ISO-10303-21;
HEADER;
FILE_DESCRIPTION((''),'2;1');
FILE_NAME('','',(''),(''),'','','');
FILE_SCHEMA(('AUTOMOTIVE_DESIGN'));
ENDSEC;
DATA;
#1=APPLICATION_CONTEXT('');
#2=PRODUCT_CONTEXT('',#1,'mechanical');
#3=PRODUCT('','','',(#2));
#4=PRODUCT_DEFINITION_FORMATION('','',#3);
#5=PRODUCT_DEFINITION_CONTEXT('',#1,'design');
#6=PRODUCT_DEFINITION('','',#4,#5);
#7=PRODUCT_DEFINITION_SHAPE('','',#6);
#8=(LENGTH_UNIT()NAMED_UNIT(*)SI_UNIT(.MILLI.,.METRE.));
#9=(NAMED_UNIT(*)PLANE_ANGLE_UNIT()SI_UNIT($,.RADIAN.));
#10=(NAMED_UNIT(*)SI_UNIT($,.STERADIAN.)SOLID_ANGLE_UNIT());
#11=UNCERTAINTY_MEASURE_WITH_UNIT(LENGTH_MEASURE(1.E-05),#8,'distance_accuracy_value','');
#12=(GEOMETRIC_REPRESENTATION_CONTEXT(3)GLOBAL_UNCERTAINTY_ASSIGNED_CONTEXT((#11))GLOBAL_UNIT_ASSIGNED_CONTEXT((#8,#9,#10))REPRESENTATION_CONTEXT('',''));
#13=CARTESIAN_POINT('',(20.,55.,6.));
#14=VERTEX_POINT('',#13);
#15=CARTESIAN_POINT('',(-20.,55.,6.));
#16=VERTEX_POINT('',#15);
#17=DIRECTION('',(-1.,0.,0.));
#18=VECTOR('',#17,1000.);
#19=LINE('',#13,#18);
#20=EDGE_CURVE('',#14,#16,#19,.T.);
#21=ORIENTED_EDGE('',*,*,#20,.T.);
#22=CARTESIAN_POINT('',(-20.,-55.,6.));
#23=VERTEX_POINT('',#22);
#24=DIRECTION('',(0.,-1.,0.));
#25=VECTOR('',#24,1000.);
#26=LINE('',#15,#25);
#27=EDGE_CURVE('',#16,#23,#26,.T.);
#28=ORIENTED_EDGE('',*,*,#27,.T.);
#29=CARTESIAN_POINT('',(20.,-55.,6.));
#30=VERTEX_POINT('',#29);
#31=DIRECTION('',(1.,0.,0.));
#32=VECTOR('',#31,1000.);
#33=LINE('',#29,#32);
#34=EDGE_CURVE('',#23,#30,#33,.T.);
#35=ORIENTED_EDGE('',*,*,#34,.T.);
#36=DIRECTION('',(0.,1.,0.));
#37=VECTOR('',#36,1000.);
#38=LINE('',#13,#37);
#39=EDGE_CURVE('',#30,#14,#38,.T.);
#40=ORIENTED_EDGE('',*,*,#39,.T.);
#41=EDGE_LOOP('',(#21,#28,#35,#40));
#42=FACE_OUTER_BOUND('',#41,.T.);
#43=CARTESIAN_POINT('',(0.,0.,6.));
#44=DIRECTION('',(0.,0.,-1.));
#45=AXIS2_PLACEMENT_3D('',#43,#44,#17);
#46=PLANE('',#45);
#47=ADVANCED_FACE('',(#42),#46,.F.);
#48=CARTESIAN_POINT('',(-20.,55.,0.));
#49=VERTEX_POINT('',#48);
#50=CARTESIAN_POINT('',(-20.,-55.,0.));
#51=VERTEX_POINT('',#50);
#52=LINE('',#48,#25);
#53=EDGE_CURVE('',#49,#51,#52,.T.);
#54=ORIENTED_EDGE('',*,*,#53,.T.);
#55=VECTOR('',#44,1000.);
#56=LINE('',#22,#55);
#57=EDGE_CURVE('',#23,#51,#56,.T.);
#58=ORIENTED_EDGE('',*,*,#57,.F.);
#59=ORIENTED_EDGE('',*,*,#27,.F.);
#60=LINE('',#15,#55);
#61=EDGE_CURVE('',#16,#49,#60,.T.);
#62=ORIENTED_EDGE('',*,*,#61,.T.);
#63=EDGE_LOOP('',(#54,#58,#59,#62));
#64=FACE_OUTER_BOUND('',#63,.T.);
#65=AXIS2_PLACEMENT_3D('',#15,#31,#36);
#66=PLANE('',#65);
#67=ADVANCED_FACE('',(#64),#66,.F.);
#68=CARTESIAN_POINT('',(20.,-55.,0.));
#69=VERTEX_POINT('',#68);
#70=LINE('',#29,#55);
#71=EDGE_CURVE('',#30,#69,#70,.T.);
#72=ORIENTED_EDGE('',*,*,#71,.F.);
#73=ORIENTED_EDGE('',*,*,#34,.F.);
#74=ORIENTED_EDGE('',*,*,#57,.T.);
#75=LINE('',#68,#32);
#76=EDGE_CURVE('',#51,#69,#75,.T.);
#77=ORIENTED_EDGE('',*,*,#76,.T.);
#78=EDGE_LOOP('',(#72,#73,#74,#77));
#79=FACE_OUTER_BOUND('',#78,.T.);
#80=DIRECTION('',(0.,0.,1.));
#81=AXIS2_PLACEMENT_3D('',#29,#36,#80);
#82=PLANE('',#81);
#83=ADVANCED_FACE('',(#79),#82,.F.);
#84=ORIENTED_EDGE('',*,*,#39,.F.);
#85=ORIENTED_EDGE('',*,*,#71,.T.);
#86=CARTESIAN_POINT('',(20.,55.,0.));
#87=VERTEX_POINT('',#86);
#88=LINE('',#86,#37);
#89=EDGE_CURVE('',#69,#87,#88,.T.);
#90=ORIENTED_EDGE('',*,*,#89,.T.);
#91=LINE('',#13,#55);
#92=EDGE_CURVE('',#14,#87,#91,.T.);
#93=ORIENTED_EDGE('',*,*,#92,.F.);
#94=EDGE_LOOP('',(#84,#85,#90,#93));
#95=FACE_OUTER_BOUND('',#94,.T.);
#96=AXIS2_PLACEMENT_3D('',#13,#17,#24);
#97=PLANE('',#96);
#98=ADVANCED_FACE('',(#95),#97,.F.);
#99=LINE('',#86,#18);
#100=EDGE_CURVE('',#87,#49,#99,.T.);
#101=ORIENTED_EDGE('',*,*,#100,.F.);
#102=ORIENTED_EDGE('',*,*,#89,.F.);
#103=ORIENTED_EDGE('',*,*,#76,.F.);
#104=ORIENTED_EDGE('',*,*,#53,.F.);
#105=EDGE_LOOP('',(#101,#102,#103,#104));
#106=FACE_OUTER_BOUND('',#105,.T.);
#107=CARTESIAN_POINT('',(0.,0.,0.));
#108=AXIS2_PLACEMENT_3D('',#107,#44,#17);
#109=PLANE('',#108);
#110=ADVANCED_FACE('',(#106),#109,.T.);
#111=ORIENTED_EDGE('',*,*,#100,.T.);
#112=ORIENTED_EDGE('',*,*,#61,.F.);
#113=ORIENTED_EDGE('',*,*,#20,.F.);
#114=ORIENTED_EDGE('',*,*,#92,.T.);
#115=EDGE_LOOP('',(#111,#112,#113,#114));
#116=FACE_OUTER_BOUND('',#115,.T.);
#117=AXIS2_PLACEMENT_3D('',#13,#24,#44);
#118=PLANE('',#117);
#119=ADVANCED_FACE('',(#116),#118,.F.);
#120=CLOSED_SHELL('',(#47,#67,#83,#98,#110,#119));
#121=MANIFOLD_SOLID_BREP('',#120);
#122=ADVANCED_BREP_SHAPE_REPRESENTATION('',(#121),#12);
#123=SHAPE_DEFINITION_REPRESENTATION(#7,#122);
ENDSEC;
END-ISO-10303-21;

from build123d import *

# Parameters (mm, degrees)
SKETCH1_W           = 40
SKETCH1_H           = 110
BOSS_EXTRUDE1_DEPTH = 6


with BuildPart() as part:
    # Sketch1 → Boss-Extrude1 (new body)
    with BuildSketch(Plane.XY):
        Rectangle(SKETCH1_W, SKETCH1_H)
    extrude(amount=BOSS_EXTRUDE1_DEPTH)


solid = part.part
